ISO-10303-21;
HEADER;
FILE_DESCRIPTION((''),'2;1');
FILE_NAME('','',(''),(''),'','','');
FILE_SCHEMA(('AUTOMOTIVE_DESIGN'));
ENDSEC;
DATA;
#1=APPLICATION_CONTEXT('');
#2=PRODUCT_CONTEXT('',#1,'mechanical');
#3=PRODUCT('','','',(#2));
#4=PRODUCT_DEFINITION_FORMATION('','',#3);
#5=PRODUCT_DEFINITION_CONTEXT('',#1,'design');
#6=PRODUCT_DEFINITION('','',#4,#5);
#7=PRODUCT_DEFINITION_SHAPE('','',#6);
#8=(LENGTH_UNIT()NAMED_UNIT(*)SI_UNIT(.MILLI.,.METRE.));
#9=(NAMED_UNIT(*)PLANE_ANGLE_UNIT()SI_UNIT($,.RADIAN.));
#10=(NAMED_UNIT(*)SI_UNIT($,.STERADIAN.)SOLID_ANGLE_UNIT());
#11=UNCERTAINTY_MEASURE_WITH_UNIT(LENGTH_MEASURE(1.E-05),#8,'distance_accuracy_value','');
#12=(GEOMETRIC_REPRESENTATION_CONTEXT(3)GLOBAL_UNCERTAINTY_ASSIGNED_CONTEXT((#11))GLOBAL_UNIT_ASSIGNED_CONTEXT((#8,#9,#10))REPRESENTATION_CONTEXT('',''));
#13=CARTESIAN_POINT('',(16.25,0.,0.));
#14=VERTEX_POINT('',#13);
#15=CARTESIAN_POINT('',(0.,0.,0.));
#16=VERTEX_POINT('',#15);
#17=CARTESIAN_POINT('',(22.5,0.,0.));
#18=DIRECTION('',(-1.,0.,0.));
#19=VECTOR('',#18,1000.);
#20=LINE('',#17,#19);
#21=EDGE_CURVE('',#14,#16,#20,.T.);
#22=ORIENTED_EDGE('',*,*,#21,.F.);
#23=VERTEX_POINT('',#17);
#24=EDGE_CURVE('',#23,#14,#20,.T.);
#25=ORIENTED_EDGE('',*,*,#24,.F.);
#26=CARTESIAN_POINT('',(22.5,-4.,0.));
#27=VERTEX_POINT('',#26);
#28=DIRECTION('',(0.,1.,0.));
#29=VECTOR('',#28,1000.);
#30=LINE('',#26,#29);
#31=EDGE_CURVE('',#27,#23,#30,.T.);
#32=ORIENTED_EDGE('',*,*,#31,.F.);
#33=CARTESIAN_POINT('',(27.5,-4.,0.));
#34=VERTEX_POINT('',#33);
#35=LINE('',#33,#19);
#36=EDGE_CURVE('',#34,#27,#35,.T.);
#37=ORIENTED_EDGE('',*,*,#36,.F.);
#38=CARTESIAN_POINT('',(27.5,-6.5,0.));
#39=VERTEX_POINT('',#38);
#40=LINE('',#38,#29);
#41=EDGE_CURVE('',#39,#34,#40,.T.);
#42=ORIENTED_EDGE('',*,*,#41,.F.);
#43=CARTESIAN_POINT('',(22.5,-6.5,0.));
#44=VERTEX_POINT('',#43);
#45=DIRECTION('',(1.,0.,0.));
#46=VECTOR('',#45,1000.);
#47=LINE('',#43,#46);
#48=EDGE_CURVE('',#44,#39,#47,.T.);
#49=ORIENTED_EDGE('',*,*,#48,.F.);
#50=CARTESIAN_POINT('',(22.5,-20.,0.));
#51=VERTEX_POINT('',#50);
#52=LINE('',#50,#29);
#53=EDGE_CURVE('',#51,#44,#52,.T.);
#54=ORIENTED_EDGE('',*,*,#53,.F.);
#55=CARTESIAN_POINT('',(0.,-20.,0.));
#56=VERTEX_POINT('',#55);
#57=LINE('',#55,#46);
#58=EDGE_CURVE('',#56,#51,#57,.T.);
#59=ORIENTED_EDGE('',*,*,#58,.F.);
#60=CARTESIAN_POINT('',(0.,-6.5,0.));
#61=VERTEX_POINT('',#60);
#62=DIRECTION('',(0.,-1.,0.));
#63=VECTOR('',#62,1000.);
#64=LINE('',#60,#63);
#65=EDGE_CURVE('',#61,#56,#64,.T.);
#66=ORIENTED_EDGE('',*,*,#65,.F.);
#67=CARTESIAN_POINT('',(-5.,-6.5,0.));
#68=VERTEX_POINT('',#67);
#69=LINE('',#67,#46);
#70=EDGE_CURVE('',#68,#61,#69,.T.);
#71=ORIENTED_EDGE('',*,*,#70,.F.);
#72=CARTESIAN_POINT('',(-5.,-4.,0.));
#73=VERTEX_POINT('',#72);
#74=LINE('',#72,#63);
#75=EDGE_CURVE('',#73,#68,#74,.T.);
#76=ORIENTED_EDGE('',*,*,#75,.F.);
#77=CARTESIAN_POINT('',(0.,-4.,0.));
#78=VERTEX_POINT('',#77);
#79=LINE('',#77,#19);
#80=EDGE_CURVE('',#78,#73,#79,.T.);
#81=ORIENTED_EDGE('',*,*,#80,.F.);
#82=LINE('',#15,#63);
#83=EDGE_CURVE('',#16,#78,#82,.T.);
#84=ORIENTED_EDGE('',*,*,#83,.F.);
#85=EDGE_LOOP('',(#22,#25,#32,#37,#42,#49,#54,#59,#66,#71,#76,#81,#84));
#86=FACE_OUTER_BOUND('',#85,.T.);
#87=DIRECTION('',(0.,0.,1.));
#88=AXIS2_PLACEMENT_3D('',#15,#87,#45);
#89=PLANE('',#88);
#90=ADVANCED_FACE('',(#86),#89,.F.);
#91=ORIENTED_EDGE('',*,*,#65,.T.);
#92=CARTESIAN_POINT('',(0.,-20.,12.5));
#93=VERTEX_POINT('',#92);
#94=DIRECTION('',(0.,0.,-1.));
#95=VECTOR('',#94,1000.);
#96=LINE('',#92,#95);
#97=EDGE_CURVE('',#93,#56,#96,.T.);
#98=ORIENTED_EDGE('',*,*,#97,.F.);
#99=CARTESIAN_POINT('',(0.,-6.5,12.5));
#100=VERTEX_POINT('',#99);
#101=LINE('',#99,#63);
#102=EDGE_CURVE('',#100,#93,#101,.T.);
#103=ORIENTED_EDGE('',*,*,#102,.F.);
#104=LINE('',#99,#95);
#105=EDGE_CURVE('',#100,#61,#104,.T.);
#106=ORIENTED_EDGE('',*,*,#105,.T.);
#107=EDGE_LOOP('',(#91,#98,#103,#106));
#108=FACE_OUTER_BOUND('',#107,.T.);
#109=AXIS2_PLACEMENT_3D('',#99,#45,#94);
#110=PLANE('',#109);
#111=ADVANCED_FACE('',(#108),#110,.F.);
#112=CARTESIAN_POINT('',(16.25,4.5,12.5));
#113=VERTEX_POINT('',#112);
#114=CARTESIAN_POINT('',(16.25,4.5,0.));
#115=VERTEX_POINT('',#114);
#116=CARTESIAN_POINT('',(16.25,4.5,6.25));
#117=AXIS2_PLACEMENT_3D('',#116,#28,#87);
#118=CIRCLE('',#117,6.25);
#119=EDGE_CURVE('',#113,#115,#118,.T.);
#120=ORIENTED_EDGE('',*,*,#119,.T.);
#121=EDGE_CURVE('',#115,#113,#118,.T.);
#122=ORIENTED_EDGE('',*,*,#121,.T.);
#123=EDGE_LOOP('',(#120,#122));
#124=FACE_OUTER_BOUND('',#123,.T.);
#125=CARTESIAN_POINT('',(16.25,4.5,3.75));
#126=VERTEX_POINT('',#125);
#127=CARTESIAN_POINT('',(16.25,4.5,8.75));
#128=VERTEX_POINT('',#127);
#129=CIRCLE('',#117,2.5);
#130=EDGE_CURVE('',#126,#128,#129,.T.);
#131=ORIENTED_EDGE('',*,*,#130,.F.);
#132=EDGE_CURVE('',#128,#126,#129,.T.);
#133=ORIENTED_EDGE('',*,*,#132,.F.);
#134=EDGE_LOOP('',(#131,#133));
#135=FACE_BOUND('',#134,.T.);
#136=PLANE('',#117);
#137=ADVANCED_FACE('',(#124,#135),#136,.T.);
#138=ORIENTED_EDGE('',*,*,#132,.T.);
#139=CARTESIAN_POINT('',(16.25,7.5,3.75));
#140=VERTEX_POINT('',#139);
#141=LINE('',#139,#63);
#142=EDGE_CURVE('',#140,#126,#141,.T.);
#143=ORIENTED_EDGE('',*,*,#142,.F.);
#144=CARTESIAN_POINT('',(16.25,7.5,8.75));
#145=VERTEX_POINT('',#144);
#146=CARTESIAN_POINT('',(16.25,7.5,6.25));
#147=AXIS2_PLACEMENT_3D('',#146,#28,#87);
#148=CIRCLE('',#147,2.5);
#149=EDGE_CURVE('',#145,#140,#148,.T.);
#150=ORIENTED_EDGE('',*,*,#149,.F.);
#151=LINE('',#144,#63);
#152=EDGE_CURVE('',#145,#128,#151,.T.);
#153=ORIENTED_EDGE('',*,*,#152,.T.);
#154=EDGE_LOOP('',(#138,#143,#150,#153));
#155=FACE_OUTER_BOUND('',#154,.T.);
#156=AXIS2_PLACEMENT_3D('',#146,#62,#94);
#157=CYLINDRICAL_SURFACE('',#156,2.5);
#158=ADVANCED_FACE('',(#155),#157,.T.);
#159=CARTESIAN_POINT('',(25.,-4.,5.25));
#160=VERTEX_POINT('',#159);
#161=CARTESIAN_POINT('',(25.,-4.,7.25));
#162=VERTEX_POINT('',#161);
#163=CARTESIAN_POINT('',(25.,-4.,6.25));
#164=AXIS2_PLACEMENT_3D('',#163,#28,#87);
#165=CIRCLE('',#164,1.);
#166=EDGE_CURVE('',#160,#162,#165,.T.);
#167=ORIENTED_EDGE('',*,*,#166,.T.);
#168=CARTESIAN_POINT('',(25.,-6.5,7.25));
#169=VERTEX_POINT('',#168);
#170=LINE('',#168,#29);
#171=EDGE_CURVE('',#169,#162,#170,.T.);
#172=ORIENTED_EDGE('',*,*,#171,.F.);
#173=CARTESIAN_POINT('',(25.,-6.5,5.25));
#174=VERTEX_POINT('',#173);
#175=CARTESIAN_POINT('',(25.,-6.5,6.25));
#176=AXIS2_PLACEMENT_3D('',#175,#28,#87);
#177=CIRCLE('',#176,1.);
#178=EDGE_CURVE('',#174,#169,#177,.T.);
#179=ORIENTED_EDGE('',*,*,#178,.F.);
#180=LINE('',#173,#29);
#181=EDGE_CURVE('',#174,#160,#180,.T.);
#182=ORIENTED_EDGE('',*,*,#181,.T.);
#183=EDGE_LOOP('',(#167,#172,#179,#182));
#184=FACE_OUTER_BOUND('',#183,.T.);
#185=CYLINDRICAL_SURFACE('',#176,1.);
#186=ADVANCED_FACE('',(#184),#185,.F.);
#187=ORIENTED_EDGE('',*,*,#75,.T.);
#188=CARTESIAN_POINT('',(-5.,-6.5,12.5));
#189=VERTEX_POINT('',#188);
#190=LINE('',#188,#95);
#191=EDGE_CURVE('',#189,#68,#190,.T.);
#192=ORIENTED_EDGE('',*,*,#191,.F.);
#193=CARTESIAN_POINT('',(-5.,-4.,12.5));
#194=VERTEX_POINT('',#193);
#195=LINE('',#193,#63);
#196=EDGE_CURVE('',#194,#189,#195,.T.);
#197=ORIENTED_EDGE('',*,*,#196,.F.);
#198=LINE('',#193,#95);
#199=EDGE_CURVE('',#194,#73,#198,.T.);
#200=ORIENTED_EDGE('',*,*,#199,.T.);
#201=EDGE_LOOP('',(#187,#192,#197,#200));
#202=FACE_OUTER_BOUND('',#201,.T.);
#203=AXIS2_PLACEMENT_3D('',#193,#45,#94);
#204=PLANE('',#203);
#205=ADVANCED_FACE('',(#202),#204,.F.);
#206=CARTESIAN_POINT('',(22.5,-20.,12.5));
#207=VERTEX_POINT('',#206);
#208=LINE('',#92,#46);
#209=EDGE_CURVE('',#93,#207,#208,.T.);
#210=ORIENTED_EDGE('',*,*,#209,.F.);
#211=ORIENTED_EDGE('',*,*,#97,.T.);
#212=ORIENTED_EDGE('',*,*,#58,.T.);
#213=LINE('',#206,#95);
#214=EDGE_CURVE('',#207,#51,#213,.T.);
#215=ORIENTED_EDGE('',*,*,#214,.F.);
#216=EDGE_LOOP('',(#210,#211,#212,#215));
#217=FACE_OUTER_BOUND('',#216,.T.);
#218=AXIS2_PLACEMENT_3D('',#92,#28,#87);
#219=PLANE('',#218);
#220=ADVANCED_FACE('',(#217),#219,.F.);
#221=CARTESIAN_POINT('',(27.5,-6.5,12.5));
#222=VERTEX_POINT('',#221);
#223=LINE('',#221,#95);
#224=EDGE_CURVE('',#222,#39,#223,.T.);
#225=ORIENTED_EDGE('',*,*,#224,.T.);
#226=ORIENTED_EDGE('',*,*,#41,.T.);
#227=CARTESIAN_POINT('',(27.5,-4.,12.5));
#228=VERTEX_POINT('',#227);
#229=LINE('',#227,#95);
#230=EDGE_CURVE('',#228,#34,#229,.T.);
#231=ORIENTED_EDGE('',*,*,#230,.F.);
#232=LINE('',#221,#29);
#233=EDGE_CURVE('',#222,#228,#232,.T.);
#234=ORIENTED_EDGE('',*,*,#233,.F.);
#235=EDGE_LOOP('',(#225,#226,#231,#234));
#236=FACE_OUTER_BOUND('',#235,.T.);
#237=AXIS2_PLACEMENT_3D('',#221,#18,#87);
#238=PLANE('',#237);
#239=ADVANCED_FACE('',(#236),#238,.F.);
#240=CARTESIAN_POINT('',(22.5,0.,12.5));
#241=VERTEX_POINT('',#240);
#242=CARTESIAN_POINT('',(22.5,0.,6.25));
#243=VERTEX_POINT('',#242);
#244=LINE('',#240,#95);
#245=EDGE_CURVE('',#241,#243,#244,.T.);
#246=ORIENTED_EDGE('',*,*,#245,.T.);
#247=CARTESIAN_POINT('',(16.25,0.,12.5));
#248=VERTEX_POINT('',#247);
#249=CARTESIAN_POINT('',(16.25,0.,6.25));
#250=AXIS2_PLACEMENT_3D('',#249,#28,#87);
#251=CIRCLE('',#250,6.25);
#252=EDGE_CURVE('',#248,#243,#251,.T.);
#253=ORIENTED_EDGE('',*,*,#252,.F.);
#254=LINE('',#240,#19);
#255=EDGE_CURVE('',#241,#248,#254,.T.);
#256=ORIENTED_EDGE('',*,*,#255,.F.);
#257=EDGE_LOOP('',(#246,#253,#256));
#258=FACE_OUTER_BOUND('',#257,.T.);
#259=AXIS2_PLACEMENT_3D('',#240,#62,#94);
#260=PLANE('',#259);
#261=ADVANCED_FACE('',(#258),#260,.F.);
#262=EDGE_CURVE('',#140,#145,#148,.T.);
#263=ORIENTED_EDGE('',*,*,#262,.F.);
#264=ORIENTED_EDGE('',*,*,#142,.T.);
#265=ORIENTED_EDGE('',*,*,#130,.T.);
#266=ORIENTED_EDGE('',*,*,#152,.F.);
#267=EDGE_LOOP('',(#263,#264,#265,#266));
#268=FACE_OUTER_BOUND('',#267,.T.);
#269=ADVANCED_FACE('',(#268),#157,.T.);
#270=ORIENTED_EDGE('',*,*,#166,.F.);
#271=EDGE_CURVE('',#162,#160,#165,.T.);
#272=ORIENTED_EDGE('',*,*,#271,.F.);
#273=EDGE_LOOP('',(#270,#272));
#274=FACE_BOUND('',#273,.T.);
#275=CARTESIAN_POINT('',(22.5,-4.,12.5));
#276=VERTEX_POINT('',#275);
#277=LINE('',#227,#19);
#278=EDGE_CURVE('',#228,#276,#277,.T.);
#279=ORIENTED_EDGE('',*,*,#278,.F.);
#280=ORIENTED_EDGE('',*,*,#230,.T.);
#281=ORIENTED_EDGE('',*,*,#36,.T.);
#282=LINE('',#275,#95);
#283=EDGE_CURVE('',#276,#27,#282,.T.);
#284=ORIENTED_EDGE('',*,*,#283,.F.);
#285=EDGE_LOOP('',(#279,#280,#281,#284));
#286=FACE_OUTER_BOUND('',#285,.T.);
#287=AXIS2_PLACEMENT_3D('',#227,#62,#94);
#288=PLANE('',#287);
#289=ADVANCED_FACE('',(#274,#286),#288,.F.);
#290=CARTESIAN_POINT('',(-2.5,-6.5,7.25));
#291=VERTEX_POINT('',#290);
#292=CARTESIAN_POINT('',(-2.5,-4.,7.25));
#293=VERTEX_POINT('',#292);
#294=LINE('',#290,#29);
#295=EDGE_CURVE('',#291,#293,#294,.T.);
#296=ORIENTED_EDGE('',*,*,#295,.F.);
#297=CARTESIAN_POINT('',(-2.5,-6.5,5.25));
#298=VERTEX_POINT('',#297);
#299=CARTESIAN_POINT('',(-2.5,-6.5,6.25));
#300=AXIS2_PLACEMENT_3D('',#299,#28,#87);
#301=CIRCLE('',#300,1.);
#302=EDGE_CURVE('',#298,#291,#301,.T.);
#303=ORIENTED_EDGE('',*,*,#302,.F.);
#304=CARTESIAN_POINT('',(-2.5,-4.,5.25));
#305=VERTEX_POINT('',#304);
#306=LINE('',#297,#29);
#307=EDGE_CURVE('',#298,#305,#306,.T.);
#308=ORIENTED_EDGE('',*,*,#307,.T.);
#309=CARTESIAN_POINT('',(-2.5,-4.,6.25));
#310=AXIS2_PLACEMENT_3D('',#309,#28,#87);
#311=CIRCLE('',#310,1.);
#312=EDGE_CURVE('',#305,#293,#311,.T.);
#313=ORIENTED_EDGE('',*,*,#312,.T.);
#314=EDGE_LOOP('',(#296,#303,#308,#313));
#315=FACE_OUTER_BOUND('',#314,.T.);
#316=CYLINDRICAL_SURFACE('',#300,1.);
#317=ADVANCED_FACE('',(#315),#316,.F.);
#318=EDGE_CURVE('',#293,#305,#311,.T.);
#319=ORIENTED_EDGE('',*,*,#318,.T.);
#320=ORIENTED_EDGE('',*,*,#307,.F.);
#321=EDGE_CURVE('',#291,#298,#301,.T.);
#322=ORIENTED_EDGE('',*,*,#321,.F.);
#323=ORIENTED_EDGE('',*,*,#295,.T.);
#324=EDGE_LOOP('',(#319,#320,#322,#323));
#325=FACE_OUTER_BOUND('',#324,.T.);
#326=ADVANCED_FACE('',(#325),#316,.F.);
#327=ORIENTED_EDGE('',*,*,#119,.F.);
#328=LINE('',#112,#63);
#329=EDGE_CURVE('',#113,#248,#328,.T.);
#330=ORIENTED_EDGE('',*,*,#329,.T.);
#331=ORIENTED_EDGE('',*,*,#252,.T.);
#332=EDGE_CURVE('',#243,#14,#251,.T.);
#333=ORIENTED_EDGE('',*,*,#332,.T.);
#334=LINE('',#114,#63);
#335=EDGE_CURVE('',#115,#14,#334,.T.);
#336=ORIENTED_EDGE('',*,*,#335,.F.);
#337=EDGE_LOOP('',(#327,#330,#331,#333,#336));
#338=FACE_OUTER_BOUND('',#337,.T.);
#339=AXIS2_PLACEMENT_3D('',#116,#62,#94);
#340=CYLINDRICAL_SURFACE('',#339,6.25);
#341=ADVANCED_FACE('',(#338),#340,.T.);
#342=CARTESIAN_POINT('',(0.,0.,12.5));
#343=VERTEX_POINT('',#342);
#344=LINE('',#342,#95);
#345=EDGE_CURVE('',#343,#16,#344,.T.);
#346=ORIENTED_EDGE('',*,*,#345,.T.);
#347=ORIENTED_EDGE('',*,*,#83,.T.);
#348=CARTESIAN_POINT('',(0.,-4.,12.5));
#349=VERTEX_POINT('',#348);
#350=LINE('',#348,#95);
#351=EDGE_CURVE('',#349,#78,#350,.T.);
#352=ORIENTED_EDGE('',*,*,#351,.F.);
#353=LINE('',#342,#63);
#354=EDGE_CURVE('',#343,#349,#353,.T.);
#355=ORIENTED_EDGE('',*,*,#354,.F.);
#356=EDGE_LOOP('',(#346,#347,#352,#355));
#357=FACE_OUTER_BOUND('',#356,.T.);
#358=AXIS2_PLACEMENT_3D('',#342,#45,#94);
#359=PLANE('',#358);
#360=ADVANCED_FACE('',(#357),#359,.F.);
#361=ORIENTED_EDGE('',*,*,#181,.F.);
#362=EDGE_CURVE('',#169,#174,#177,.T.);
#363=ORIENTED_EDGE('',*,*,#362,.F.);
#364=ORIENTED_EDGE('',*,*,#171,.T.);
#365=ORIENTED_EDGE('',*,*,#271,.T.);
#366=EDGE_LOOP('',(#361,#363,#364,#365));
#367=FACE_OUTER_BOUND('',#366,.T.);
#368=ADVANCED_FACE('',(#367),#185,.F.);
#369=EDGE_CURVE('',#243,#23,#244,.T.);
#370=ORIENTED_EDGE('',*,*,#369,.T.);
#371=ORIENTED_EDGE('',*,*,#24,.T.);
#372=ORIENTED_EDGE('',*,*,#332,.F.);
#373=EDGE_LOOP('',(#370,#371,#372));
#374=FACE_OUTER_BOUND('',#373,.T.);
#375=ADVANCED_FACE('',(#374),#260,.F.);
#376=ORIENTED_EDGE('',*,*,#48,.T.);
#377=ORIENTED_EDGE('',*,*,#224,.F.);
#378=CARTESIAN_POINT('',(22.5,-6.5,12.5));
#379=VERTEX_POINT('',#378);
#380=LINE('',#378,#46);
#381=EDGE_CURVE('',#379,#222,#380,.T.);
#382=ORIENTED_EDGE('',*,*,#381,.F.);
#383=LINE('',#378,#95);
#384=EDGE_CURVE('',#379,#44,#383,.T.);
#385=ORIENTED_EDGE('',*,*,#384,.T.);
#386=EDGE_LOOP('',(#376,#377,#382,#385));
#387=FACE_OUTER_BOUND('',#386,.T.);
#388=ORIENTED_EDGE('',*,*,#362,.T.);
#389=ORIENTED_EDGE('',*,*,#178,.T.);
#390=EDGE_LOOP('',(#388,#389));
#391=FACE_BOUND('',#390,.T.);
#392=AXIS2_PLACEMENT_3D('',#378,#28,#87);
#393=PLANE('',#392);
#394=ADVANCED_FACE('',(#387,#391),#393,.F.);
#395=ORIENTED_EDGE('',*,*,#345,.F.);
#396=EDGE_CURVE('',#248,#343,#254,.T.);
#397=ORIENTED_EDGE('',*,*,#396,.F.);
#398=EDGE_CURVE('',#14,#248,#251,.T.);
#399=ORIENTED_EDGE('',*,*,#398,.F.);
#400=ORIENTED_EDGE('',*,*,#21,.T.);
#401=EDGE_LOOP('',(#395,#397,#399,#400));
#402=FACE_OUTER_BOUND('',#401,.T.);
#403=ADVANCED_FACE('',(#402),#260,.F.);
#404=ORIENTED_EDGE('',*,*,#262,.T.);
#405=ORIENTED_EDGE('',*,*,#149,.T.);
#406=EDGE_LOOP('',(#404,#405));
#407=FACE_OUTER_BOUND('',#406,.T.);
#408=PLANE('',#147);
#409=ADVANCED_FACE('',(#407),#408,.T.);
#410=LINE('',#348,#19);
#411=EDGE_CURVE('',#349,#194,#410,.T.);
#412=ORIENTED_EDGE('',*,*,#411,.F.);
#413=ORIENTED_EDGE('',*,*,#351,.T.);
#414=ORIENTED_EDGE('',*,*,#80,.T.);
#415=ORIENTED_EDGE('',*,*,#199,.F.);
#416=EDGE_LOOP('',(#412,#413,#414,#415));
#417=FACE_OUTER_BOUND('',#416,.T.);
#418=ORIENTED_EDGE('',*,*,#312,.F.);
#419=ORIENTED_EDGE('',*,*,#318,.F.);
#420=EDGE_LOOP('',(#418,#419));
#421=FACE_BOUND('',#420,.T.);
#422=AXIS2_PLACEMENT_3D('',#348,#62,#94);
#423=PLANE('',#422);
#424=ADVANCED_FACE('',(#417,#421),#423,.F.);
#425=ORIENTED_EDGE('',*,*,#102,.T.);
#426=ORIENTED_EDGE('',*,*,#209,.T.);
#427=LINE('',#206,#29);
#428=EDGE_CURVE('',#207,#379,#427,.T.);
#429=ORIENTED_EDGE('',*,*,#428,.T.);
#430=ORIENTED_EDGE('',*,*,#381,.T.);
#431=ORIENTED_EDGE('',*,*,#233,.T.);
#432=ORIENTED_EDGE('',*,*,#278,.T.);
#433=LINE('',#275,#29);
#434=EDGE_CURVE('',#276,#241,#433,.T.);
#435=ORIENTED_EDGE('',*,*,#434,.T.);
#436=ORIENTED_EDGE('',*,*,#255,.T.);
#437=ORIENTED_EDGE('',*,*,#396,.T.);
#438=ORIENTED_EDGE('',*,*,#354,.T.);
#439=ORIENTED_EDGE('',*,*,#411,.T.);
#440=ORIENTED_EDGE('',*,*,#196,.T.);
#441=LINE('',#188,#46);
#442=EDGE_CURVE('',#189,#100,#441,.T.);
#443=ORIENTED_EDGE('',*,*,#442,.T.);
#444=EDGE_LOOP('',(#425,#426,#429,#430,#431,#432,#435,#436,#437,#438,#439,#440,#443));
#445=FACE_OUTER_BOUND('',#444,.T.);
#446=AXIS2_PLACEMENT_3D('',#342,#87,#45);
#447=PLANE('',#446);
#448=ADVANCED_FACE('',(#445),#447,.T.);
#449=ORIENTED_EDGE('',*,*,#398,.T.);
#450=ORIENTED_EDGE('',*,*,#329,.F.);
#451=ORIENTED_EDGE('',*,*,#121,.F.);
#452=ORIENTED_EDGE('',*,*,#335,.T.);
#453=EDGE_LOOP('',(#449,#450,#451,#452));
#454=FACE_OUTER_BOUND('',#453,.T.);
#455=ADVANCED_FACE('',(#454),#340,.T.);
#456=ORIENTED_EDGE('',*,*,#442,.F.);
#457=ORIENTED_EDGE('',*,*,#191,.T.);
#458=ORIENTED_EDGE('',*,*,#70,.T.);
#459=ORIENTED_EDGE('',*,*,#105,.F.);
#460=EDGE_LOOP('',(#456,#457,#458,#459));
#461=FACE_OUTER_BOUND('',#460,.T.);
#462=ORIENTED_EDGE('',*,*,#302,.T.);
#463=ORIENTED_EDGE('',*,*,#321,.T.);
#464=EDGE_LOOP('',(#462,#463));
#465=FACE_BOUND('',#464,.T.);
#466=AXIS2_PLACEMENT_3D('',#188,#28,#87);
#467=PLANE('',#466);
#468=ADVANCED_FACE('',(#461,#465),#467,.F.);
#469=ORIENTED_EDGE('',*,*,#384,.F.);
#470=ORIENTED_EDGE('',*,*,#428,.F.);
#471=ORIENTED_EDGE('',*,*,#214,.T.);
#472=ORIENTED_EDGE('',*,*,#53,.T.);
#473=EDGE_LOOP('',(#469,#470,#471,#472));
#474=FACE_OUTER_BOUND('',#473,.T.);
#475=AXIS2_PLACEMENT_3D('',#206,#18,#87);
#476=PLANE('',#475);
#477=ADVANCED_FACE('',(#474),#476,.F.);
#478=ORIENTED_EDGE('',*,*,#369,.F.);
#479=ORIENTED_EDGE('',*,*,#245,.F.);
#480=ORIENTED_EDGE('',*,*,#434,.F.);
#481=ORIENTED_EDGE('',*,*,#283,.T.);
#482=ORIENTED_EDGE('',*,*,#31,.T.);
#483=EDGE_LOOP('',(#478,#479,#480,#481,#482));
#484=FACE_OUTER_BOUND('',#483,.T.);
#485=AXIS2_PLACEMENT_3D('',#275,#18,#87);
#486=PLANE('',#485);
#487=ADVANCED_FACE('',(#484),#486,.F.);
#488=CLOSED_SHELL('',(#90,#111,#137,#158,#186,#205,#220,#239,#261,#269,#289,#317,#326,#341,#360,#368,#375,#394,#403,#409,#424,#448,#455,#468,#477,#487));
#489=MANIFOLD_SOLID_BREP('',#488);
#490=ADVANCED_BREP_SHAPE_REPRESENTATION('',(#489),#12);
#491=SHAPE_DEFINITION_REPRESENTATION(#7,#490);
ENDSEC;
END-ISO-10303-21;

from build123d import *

# Parameters (mm, degrees)
SERVO_CASE_WITH_MOUNTING_TABS_DEPTH = 12.5
TAB_MOUNTING_HOLE_SKETCH_R          = 1
TAB_MOUNTING_HOLE_DEPTH             = 2.5
OUTPUT_GEAR_BOSS_SKETCH_12_5_R      = 6.25
OUTPUT_GEAR_BOSS_12_5_DEPTH         = 4.5
OUTPUT_SHAFT_SKETCH_5_R             = 2.5
OUTPUT_SHAFT_5_DEPTH                = 3


with BuildPart() as part:
    # Servo Case Profile Sketch → Servo Case with Mounting Tabs (new body)
    with BuildSketch(Plane.XY):
        Polygon((0, 0), (0, -4), (-5, -4), (-5, -6.5), (0, -6.5), (0, -20), (22.5, -20), (22.5, -6.5), (27.5, -6.5), (27.5, -4), (22.5, -4), (22.5, 0), align=None)
    extrude(amount=SERVO_CASE_WITH_MOUNTING_TABS_DEPTH)

    # Tab Mounting Hole Sketch → Tab Mounting Hole (cut)
    with BuildSketch(Plane(origin=(0, -4, 0), x_dir=(1, 0, 0), z_dir=(0, 1, 0))):
        with Locations(Location((25, -6.25, 0), (0, 0, 270))):
            Circle(TAB_MOUNTING_HOLE_SKETCH_R)
        with Locations(Location((-2.5, -6.25, 0), (0, 0, 270))):
            Circle(TAB_MOUNTING_HOLE_SKETCH_R)
    extrude(amount=-TAB_MOUNTING_HOLE_DEPTH, mode=Mode.SUBTRACT)

    # Output Gear Boss Sketch Ø12.5 → Output Gear Boss Ø12.5 (add)
    with BuildSketch(Plane(origin=(0, 0, 0), x_dir=(1, 0, 0), z_dir=(0, 1, 0))):
        with Locations(Location((16.25, -6.25, 0), (0, 0, 270))):
            Circle(OUTPUT_GEAR_BOSS_SKETCH_12_5_R)
    extrude(amount=OUTPUT_GEAR_BOSS_12_5_DEPTH)

    # Output Shaft Sketch Ø5 → Output Shaft Ø5 (add)
    with BuildSketch(Plane(origin=(0, 4.5, 0), x_dir=(1, 0, 0), z_dir=(0, 1, 0))):
        with Locations(Location((16.25, -6.25, 0), (0, 0, 270))):
            Circle(OUTPUT_SHAFT_SKETCH_5_R)
    extrude(amount=OUTPUT_SHAFT_5_DEPTH)


solid = part.part
